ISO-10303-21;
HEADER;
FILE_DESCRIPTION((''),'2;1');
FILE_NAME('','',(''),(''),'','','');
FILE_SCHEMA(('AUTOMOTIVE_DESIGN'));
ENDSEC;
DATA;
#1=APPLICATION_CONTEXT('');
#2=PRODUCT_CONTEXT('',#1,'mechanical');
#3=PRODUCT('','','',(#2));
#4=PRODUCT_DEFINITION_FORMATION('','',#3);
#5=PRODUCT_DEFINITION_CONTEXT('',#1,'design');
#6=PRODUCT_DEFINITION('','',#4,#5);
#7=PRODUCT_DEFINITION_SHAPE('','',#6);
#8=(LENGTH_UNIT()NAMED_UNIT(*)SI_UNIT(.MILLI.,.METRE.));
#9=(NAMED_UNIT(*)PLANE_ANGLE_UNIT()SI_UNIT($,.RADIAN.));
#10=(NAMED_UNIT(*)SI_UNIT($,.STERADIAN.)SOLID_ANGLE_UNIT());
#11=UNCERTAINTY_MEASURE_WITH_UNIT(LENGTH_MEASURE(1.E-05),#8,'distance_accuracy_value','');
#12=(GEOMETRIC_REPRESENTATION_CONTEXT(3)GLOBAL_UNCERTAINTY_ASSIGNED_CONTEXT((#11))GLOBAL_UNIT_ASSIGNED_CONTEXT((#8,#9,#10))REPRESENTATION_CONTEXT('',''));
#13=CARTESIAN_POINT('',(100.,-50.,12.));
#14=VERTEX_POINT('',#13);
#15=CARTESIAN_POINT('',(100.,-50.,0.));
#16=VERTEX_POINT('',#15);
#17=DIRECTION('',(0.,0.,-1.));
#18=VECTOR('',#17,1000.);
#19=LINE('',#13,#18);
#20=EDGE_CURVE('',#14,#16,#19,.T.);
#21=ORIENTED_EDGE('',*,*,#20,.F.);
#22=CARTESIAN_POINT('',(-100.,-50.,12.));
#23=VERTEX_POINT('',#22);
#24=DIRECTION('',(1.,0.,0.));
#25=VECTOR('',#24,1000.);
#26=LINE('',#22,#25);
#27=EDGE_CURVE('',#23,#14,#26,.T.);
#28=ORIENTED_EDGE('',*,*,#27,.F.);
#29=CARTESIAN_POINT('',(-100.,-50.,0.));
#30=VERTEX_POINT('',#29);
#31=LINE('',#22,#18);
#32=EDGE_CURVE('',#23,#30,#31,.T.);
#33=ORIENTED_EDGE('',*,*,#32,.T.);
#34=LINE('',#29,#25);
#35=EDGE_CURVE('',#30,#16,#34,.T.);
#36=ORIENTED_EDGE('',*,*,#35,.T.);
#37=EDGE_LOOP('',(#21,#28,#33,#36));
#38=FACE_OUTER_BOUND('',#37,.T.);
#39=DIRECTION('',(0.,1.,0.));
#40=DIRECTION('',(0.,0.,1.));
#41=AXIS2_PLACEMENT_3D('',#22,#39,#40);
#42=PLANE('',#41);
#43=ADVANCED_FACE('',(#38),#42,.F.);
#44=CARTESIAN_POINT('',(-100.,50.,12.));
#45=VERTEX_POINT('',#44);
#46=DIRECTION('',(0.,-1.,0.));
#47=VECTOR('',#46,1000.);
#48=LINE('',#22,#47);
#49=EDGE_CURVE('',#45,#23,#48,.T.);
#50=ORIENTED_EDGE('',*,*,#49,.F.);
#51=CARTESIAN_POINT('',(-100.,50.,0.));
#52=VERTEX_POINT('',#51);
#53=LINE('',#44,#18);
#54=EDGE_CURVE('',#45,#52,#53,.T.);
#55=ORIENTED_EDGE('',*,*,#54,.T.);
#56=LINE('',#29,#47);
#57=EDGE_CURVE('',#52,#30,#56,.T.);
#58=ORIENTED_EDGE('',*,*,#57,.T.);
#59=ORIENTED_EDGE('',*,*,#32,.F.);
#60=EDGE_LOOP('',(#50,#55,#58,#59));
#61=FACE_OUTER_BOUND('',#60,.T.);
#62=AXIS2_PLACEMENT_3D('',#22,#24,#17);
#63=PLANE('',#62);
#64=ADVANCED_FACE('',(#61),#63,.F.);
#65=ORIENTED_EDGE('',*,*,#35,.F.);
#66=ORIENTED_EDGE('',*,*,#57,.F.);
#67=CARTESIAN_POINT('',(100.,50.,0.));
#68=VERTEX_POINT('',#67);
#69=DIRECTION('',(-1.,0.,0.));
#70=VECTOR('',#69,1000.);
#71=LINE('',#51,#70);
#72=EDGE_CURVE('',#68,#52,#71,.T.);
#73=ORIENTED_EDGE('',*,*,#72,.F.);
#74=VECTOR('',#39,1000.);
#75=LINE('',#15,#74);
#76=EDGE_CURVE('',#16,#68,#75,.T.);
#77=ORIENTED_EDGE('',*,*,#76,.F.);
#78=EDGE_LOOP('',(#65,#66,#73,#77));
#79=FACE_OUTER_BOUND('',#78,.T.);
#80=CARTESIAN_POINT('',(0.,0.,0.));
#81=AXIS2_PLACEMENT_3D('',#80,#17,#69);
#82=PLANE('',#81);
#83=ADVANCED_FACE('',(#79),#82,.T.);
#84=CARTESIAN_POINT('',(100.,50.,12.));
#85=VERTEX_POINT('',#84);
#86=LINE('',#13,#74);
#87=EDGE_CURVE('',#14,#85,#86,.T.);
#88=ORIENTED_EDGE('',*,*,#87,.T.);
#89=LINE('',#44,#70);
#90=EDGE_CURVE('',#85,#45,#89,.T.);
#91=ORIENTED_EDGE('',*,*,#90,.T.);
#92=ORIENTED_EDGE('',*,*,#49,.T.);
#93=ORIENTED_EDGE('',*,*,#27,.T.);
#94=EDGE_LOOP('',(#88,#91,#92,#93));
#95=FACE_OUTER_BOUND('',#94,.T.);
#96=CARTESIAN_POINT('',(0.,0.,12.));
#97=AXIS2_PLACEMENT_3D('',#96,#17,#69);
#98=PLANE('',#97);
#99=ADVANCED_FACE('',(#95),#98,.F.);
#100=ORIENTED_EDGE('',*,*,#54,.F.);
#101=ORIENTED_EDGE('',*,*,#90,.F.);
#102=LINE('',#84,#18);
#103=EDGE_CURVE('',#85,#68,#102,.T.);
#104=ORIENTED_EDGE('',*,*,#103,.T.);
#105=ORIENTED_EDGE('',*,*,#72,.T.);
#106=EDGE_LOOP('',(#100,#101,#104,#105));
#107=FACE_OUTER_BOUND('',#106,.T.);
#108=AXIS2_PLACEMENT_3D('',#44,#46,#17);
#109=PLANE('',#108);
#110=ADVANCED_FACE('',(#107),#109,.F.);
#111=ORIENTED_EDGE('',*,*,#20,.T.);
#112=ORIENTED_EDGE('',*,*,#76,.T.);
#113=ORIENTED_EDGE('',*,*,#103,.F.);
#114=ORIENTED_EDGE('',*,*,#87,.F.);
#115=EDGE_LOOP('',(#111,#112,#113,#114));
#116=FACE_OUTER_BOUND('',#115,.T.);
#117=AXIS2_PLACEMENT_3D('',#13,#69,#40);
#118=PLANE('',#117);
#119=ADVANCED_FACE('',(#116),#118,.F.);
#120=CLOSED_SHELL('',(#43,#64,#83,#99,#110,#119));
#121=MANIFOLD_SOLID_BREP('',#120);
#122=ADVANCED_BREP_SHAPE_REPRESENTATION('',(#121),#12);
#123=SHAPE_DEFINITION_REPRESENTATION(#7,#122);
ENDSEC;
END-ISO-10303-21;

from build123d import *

# Parameters (mm, degrees)
SKETCH_1_W      = 200
SKETCH_1_H      = 100
EXTRUDE_1_DEPTH = 12


with BuildPart() as part:
    # 草图1 → 凸台-拉伸1 (new body)
    with BuildSketch(Plane.XY):
        Rectangle(SKETCH_1_W, SKETCH_1_H)
    extrude(amount=EXTRUDE_1_DEPTH)


solid = part.part
